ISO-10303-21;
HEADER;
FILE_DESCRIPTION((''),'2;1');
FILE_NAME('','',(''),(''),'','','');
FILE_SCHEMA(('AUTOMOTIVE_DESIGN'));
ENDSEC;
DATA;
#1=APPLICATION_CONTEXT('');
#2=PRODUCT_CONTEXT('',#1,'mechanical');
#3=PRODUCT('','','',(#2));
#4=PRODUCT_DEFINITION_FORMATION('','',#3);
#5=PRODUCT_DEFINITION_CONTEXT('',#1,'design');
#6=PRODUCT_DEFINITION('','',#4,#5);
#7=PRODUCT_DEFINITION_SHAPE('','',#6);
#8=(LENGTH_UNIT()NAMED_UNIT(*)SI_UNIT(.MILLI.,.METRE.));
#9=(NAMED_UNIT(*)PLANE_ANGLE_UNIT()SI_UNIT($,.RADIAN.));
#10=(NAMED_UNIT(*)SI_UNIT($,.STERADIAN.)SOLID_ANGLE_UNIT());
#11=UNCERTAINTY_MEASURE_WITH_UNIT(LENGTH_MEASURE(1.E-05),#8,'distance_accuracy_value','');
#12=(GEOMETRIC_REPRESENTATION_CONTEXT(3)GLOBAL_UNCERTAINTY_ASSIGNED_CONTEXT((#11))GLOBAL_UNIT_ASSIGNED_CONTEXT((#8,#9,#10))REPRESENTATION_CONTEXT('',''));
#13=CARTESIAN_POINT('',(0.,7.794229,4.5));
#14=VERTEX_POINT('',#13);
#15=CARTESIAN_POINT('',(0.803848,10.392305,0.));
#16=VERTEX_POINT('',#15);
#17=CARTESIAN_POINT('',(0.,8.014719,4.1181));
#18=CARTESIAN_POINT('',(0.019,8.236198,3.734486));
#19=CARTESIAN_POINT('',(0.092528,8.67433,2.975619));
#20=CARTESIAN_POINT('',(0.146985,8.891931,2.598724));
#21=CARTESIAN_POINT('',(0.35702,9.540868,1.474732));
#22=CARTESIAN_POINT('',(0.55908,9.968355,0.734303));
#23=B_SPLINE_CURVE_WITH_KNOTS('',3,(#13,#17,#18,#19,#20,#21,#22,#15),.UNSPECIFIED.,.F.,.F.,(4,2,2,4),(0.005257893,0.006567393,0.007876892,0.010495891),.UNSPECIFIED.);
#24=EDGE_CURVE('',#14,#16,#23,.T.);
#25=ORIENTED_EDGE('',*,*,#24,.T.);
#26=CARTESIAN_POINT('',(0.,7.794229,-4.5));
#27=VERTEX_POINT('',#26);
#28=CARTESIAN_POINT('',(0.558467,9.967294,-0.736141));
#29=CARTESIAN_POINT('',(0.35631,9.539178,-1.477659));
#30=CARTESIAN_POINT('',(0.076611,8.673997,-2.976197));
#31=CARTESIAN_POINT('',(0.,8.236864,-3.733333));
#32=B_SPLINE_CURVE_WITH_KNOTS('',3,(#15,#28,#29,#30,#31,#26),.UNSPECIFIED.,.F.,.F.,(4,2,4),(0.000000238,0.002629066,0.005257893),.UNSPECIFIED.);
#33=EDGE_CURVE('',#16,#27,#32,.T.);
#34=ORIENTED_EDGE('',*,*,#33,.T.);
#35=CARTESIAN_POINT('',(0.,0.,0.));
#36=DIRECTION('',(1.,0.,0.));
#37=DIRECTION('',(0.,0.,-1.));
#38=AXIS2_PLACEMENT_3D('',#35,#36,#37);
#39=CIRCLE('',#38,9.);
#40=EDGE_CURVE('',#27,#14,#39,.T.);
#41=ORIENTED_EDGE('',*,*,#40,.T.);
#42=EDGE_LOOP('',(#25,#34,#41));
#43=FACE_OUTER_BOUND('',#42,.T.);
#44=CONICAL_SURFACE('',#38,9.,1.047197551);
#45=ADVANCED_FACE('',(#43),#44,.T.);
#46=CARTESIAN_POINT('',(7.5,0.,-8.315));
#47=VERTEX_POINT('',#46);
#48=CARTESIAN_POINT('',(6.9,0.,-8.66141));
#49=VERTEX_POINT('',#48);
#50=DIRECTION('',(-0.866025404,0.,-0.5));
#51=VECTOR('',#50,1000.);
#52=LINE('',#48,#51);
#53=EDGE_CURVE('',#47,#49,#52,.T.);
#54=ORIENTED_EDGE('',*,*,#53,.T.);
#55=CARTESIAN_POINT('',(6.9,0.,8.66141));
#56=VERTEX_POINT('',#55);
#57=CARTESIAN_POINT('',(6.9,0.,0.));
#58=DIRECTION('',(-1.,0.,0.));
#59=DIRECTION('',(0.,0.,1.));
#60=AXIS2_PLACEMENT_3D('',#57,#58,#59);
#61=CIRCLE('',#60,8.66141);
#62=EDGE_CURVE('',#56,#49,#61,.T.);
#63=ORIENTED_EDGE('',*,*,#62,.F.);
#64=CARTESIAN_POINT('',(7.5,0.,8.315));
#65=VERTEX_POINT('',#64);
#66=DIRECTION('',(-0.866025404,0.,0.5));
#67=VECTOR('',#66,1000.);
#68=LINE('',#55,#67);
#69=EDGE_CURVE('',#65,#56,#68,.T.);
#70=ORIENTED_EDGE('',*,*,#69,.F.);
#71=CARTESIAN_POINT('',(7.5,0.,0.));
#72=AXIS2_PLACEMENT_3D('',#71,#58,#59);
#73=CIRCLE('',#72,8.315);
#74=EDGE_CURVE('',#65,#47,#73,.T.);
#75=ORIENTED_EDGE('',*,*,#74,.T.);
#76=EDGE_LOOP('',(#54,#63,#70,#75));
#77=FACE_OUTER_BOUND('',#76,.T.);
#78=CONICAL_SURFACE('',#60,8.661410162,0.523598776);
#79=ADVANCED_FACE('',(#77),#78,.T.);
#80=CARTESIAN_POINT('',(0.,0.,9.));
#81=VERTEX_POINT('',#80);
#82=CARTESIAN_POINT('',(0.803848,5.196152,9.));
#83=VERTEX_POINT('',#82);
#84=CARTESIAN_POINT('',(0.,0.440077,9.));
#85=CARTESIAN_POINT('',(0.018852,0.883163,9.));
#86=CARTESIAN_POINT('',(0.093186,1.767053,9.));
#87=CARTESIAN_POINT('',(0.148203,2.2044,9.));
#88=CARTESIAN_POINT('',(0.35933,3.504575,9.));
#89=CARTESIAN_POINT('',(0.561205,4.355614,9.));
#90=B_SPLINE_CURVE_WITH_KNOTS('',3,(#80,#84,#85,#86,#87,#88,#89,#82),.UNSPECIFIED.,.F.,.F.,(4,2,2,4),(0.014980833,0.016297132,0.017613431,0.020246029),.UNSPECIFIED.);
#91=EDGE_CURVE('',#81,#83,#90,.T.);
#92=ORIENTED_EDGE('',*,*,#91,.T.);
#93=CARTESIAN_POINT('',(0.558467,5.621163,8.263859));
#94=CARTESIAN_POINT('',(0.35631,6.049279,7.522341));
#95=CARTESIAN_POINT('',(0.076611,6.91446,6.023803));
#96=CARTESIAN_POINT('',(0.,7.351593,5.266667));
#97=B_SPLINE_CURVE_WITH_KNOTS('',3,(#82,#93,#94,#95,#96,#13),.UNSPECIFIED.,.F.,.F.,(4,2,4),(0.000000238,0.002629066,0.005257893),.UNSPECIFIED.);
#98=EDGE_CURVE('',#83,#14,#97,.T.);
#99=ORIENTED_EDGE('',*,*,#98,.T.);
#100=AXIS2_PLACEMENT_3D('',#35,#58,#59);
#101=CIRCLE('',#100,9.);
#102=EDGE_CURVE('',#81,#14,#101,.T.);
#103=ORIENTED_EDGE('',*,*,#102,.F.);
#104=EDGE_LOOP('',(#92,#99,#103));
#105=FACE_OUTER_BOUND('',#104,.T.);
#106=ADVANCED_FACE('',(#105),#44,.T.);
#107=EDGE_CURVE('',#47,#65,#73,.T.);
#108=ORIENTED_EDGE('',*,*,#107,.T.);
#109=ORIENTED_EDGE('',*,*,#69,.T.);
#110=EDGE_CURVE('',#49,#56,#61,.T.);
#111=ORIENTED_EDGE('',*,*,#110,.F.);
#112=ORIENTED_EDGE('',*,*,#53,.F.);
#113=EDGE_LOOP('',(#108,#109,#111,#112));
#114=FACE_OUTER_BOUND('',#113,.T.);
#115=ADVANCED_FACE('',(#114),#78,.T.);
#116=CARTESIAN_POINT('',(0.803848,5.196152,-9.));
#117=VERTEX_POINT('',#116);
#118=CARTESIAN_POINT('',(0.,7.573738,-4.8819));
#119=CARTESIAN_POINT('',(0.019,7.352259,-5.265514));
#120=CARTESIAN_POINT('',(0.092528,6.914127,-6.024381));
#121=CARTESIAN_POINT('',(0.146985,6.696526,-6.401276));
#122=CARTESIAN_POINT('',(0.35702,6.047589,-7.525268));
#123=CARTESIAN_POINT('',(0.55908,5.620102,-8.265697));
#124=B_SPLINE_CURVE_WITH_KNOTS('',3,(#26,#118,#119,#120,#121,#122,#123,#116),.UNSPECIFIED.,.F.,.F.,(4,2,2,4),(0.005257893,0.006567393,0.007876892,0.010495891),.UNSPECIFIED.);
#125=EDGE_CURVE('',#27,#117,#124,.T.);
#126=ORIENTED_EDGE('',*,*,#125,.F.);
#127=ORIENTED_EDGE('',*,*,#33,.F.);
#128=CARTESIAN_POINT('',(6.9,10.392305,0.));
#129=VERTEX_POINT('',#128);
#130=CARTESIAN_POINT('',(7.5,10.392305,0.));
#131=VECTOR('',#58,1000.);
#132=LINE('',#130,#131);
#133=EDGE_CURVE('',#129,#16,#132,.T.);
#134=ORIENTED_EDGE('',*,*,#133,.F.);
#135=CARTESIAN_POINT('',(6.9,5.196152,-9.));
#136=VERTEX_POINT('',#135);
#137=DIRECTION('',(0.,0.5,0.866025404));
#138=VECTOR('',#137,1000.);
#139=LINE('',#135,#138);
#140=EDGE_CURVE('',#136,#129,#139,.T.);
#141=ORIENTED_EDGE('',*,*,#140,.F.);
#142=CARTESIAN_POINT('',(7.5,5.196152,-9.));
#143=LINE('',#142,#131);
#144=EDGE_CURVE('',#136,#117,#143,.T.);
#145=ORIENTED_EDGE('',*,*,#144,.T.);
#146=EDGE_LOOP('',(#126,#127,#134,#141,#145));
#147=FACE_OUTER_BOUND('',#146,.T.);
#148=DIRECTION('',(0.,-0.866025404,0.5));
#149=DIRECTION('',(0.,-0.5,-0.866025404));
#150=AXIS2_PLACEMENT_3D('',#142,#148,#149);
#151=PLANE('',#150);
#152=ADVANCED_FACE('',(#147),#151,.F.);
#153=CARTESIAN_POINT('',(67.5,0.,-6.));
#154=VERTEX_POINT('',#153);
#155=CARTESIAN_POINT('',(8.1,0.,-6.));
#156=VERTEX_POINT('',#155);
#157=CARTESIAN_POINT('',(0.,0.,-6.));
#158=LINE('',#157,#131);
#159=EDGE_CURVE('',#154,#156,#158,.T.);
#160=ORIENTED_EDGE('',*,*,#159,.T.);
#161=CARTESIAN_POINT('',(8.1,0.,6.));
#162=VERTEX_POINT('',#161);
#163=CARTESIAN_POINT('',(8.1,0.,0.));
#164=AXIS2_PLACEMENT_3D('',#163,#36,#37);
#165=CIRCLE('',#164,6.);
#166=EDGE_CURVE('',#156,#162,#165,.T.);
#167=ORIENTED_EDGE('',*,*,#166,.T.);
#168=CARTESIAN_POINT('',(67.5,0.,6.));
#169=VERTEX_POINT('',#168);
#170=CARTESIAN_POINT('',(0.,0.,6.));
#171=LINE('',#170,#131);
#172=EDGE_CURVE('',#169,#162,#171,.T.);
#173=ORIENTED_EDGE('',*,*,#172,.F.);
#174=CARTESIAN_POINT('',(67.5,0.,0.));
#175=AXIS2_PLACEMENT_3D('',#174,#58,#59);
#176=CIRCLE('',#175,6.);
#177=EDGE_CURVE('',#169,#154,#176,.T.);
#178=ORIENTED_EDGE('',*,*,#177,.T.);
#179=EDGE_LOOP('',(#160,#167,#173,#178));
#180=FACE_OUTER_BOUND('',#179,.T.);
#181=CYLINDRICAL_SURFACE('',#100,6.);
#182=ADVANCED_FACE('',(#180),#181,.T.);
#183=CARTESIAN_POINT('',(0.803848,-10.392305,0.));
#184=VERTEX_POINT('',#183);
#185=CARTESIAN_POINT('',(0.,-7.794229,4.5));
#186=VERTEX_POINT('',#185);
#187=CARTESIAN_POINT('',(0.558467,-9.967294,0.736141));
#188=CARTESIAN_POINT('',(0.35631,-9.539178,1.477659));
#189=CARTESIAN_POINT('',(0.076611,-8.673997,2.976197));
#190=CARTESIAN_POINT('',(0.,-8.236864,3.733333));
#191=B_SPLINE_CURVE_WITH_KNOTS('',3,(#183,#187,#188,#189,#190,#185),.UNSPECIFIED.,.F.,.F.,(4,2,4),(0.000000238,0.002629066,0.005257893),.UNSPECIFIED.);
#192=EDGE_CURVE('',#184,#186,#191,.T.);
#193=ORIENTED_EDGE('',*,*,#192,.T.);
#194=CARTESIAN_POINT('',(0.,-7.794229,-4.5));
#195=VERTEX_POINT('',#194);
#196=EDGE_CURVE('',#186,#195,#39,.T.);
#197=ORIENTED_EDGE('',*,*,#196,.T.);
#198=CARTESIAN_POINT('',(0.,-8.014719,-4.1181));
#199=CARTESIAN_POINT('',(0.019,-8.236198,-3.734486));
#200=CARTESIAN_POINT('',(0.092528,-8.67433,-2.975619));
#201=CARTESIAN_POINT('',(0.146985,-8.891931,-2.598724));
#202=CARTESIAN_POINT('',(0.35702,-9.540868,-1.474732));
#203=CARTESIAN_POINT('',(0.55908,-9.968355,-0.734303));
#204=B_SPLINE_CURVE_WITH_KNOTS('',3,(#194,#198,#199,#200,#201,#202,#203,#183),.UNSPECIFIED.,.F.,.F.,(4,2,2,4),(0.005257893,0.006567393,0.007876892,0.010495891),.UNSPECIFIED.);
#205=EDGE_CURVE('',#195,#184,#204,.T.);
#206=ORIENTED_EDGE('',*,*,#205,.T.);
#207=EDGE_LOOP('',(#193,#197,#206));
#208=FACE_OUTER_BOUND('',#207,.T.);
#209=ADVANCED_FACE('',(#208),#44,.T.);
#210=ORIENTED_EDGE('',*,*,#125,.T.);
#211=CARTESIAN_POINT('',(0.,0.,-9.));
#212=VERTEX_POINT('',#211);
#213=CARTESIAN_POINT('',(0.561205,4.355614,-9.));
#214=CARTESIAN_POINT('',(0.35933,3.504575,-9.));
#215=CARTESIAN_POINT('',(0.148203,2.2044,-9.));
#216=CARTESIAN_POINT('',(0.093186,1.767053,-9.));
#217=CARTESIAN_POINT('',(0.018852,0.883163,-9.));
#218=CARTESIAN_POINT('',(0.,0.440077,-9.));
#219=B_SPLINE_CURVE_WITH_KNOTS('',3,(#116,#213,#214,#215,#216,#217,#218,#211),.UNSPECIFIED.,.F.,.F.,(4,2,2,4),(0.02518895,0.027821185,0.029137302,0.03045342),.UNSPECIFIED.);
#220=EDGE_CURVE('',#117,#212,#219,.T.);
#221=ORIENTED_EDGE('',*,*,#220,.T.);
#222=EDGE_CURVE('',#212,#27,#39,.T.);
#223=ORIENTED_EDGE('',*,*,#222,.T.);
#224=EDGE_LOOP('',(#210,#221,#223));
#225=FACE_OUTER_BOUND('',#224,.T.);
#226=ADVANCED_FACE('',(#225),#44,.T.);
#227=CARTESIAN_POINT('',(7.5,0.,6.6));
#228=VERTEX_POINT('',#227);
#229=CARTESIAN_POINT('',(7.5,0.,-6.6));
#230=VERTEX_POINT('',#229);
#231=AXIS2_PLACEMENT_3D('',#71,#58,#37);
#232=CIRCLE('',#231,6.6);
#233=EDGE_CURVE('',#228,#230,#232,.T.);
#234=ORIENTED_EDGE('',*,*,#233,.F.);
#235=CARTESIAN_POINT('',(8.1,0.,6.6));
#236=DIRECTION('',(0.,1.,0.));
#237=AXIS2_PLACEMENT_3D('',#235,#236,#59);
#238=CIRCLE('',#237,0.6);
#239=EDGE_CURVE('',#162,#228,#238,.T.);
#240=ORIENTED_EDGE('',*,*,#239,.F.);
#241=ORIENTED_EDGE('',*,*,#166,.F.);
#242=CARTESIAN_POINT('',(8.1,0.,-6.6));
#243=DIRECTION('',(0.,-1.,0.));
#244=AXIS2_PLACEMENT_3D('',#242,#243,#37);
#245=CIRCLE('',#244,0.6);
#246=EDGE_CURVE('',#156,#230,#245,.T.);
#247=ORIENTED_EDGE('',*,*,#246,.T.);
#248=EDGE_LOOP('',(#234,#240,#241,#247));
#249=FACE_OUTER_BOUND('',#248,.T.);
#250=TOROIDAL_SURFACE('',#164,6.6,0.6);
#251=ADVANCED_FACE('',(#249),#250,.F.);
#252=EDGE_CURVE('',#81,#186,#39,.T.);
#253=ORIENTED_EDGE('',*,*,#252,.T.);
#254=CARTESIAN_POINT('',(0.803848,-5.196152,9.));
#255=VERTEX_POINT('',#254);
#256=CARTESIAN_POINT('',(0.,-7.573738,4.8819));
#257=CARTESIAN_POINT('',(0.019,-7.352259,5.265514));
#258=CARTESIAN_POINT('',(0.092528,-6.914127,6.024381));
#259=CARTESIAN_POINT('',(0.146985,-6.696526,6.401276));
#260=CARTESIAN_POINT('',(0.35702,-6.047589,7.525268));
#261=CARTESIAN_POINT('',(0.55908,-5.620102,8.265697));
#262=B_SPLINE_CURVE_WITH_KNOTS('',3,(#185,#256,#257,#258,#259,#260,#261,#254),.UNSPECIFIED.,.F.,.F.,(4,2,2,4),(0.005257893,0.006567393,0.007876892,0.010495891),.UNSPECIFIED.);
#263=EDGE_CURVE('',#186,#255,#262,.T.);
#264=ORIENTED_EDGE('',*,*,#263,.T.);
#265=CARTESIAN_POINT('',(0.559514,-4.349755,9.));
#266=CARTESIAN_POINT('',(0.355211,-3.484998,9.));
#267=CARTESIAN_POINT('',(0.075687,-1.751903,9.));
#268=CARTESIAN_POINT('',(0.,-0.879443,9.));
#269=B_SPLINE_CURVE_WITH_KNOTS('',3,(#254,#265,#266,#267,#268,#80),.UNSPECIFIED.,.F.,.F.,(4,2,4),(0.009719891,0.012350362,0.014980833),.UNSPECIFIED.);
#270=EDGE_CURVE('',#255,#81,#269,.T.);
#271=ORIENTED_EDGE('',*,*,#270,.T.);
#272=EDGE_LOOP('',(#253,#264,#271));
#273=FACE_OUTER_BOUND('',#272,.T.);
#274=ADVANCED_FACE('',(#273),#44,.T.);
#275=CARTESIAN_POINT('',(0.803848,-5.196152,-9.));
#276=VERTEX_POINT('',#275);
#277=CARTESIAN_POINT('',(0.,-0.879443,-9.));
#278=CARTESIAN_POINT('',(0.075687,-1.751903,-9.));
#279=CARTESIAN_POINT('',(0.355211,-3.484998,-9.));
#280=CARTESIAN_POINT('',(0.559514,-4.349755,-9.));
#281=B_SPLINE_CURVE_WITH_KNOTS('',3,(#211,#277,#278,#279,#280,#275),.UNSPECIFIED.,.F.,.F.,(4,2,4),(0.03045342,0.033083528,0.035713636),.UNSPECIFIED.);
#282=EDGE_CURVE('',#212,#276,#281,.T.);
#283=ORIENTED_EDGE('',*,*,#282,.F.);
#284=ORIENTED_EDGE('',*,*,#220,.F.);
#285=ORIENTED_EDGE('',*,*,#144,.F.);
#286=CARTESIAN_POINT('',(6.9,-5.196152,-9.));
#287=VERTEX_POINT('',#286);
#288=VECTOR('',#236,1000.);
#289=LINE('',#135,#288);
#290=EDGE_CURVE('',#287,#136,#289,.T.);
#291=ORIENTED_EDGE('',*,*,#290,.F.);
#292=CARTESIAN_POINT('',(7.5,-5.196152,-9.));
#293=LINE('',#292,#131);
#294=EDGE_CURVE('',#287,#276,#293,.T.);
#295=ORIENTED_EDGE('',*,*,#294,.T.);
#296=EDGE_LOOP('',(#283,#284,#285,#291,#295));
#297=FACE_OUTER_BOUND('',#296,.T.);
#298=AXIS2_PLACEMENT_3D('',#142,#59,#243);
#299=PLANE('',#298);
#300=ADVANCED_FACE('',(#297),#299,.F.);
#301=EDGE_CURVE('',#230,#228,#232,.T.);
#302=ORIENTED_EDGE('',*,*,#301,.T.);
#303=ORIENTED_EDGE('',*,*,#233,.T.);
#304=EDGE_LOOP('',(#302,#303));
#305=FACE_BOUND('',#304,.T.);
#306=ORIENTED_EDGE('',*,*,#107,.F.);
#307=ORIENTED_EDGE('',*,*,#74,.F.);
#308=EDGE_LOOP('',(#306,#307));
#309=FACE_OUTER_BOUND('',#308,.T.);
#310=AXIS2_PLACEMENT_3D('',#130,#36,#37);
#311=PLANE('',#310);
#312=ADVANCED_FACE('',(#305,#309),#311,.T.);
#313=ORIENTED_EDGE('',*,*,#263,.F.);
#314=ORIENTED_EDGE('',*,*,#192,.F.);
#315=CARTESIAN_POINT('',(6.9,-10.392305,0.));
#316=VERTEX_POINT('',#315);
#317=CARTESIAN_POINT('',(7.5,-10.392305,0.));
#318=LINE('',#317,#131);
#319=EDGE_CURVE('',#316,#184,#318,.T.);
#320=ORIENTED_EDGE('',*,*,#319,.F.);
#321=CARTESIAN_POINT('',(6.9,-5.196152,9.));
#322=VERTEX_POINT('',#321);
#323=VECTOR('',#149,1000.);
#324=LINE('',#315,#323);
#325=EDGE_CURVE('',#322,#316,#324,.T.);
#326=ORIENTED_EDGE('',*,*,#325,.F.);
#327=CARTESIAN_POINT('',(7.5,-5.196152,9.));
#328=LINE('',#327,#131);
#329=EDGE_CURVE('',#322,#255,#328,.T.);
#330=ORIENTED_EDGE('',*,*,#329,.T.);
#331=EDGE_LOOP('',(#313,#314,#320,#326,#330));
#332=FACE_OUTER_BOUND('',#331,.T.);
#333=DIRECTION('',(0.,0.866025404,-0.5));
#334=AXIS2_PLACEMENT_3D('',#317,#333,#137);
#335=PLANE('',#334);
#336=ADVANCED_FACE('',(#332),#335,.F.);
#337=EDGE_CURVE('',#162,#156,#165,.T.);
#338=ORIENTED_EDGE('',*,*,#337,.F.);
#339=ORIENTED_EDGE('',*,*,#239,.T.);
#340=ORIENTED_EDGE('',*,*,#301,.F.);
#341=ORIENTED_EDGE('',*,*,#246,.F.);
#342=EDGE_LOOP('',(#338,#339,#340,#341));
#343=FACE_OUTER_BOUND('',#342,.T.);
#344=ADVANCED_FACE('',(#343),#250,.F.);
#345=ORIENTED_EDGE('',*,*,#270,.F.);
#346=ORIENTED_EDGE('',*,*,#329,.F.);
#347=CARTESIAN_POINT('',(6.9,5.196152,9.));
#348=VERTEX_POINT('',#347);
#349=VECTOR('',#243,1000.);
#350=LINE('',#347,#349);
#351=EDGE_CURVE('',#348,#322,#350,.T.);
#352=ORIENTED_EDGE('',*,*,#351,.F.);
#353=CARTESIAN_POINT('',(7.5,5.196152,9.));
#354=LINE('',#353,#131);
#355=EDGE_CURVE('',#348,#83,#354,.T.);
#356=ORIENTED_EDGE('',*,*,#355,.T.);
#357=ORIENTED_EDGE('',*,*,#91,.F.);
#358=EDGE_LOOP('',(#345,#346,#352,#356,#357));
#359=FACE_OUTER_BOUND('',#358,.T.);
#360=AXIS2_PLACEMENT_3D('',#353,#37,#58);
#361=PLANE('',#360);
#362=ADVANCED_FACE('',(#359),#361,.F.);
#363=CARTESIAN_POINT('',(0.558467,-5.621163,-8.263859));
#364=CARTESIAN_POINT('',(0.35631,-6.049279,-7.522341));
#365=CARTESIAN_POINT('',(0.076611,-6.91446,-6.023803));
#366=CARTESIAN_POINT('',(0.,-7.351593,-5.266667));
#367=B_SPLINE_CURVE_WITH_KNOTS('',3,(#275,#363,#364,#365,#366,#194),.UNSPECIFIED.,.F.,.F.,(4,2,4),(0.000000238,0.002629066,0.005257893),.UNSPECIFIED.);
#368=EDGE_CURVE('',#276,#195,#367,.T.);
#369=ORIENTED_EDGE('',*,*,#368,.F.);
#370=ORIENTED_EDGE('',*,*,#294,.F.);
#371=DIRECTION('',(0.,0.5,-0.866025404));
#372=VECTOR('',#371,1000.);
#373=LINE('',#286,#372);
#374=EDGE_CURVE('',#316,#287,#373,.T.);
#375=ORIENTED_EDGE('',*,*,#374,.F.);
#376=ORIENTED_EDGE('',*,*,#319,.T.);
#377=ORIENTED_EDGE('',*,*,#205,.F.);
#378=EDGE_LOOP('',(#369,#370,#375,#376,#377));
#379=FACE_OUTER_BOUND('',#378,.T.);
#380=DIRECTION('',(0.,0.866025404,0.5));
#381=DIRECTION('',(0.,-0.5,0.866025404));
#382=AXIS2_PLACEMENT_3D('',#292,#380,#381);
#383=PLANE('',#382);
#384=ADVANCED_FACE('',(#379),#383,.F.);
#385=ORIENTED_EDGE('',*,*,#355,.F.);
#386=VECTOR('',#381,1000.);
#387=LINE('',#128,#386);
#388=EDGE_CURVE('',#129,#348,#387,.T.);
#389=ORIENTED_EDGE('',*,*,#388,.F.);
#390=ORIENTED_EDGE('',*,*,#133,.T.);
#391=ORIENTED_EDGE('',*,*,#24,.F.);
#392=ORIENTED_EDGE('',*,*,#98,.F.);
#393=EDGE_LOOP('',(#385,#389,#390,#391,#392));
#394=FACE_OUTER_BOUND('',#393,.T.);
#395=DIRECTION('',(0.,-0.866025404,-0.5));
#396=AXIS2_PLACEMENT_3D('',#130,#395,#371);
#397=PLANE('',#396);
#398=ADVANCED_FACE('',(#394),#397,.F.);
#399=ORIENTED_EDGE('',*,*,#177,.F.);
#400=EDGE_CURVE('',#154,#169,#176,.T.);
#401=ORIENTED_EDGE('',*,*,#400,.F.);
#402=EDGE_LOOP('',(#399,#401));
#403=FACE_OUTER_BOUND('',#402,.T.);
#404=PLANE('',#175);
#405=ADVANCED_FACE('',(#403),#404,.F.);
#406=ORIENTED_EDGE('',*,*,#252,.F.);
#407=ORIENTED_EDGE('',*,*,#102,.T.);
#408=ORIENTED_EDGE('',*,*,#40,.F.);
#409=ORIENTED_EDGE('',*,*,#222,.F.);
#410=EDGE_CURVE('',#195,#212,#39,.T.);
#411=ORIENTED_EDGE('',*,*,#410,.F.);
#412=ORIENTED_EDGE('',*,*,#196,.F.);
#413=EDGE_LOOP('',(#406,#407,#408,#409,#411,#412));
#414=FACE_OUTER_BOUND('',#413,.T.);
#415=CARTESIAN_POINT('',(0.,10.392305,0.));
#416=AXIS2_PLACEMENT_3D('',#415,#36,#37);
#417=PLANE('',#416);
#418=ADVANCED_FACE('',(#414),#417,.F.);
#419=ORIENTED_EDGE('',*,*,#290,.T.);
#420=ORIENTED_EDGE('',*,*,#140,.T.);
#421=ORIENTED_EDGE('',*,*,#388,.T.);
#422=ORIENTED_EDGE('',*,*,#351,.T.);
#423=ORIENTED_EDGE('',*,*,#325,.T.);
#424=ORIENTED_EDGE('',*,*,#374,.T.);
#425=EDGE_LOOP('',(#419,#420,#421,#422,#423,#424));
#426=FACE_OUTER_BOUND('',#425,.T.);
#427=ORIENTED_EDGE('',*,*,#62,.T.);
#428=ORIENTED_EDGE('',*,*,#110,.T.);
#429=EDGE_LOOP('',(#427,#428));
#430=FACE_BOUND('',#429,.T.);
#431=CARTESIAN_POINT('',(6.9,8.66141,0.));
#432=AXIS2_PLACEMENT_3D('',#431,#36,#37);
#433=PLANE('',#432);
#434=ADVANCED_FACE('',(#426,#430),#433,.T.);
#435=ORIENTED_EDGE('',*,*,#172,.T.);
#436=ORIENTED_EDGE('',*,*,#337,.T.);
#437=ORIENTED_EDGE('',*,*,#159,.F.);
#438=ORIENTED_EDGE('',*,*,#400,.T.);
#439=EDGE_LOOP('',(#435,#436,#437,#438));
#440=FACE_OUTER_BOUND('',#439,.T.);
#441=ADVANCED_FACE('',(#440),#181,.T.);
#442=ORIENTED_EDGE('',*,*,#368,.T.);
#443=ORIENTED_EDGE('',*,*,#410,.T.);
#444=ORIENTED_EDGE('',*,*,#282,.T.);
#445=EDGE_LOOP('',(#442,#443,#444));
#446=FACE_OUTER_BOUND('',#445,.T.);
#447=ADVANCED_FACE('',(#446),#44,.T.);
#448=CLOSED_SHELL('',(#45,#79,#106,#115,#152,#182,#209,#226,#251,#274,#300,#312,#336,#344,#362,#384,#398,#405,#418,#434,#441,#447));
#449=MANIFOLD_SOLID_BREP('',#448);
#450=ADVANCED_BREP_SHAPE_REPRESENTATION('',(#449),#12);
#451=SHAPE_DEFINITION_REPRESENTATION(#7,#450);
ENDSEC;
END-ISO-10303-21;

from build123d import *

# Parameters (mm, degrees)
EXTRUDE_387_DEPTH = 7.5
FILLET_1310_R     = 0.6


with BuildPart() as part:
    # 草图1 → Extrude 387 (new body)
    with BuildSketch(Plane(origin=(0, 0, 0), x_dir=(0, 0, -1), z_dir=(1, 0, 0))):
        Polygon((9, 5.196152423), (9, -5.196152423), (0, -10.392304845), (-9, -5.196152423), (-9, 5.196152423), (0, 10.392304845), align=None)
    extrude(amount=EXTRUDE_387_DEPTH)

    # 草图2 → 凸台-旋转1 (revolve)
    with BuildSketch(Plane.XY, mode=Mode.PRIVATE) as revolve_1_sk:
        Polygon((0, 0), (67.5, 0), (67.5, 4.4845), (67.5, 6), (37.5, 6), (0, 6), align=None)
    revolve(revolve_1_sk.sketch.rotate(Axis((0, 0, 0), (1, 0, 0)), 90), axis=Axis((0, 0, 0), (1, 0, 0)))

    # 草图3 → 切除-旋转1 (revolve, cut)
    with BuildSketch(Plane.XY):
        Polygon((0, 9), (3.690598923, 15.392304845), (3.690598923, 20.392304845), (-10, 20.392304845), (-10, 9), align=None)
    revolve(axis=Axis((0, 0, 0), (1, 0, 0)), mode=Mode.SUBTRACT)

    # 草图4 → 切除-旋转3 (revolve, cut)
    with BuildSketch(Plane.XY, mode=Mode.PRIVATE) as cut_revolve_3_sk:
        Polygon((7.5, 8.315), (6.9, 8.661410162), (6.9, 10.392304845), (7.5, 10.392304845), align=None)
    revolve(cut_revolve_3_sk.sketch.rotate(Axis((0, 0, 0), (1, 0, 0)), 90), axis=Axis((0, 0, 0), (1, 0, 0)), mode=Mode.SUBTRACT)

    # Fillet 1310
    fillet_1310_edges = [part.edges().sort_by_distance(p)[0] for p in [
        (7.5, 0, -6),
    ]]
    fillet(fillet_1310_edges, radius=FILLET_1310_R)


solid = part.part
